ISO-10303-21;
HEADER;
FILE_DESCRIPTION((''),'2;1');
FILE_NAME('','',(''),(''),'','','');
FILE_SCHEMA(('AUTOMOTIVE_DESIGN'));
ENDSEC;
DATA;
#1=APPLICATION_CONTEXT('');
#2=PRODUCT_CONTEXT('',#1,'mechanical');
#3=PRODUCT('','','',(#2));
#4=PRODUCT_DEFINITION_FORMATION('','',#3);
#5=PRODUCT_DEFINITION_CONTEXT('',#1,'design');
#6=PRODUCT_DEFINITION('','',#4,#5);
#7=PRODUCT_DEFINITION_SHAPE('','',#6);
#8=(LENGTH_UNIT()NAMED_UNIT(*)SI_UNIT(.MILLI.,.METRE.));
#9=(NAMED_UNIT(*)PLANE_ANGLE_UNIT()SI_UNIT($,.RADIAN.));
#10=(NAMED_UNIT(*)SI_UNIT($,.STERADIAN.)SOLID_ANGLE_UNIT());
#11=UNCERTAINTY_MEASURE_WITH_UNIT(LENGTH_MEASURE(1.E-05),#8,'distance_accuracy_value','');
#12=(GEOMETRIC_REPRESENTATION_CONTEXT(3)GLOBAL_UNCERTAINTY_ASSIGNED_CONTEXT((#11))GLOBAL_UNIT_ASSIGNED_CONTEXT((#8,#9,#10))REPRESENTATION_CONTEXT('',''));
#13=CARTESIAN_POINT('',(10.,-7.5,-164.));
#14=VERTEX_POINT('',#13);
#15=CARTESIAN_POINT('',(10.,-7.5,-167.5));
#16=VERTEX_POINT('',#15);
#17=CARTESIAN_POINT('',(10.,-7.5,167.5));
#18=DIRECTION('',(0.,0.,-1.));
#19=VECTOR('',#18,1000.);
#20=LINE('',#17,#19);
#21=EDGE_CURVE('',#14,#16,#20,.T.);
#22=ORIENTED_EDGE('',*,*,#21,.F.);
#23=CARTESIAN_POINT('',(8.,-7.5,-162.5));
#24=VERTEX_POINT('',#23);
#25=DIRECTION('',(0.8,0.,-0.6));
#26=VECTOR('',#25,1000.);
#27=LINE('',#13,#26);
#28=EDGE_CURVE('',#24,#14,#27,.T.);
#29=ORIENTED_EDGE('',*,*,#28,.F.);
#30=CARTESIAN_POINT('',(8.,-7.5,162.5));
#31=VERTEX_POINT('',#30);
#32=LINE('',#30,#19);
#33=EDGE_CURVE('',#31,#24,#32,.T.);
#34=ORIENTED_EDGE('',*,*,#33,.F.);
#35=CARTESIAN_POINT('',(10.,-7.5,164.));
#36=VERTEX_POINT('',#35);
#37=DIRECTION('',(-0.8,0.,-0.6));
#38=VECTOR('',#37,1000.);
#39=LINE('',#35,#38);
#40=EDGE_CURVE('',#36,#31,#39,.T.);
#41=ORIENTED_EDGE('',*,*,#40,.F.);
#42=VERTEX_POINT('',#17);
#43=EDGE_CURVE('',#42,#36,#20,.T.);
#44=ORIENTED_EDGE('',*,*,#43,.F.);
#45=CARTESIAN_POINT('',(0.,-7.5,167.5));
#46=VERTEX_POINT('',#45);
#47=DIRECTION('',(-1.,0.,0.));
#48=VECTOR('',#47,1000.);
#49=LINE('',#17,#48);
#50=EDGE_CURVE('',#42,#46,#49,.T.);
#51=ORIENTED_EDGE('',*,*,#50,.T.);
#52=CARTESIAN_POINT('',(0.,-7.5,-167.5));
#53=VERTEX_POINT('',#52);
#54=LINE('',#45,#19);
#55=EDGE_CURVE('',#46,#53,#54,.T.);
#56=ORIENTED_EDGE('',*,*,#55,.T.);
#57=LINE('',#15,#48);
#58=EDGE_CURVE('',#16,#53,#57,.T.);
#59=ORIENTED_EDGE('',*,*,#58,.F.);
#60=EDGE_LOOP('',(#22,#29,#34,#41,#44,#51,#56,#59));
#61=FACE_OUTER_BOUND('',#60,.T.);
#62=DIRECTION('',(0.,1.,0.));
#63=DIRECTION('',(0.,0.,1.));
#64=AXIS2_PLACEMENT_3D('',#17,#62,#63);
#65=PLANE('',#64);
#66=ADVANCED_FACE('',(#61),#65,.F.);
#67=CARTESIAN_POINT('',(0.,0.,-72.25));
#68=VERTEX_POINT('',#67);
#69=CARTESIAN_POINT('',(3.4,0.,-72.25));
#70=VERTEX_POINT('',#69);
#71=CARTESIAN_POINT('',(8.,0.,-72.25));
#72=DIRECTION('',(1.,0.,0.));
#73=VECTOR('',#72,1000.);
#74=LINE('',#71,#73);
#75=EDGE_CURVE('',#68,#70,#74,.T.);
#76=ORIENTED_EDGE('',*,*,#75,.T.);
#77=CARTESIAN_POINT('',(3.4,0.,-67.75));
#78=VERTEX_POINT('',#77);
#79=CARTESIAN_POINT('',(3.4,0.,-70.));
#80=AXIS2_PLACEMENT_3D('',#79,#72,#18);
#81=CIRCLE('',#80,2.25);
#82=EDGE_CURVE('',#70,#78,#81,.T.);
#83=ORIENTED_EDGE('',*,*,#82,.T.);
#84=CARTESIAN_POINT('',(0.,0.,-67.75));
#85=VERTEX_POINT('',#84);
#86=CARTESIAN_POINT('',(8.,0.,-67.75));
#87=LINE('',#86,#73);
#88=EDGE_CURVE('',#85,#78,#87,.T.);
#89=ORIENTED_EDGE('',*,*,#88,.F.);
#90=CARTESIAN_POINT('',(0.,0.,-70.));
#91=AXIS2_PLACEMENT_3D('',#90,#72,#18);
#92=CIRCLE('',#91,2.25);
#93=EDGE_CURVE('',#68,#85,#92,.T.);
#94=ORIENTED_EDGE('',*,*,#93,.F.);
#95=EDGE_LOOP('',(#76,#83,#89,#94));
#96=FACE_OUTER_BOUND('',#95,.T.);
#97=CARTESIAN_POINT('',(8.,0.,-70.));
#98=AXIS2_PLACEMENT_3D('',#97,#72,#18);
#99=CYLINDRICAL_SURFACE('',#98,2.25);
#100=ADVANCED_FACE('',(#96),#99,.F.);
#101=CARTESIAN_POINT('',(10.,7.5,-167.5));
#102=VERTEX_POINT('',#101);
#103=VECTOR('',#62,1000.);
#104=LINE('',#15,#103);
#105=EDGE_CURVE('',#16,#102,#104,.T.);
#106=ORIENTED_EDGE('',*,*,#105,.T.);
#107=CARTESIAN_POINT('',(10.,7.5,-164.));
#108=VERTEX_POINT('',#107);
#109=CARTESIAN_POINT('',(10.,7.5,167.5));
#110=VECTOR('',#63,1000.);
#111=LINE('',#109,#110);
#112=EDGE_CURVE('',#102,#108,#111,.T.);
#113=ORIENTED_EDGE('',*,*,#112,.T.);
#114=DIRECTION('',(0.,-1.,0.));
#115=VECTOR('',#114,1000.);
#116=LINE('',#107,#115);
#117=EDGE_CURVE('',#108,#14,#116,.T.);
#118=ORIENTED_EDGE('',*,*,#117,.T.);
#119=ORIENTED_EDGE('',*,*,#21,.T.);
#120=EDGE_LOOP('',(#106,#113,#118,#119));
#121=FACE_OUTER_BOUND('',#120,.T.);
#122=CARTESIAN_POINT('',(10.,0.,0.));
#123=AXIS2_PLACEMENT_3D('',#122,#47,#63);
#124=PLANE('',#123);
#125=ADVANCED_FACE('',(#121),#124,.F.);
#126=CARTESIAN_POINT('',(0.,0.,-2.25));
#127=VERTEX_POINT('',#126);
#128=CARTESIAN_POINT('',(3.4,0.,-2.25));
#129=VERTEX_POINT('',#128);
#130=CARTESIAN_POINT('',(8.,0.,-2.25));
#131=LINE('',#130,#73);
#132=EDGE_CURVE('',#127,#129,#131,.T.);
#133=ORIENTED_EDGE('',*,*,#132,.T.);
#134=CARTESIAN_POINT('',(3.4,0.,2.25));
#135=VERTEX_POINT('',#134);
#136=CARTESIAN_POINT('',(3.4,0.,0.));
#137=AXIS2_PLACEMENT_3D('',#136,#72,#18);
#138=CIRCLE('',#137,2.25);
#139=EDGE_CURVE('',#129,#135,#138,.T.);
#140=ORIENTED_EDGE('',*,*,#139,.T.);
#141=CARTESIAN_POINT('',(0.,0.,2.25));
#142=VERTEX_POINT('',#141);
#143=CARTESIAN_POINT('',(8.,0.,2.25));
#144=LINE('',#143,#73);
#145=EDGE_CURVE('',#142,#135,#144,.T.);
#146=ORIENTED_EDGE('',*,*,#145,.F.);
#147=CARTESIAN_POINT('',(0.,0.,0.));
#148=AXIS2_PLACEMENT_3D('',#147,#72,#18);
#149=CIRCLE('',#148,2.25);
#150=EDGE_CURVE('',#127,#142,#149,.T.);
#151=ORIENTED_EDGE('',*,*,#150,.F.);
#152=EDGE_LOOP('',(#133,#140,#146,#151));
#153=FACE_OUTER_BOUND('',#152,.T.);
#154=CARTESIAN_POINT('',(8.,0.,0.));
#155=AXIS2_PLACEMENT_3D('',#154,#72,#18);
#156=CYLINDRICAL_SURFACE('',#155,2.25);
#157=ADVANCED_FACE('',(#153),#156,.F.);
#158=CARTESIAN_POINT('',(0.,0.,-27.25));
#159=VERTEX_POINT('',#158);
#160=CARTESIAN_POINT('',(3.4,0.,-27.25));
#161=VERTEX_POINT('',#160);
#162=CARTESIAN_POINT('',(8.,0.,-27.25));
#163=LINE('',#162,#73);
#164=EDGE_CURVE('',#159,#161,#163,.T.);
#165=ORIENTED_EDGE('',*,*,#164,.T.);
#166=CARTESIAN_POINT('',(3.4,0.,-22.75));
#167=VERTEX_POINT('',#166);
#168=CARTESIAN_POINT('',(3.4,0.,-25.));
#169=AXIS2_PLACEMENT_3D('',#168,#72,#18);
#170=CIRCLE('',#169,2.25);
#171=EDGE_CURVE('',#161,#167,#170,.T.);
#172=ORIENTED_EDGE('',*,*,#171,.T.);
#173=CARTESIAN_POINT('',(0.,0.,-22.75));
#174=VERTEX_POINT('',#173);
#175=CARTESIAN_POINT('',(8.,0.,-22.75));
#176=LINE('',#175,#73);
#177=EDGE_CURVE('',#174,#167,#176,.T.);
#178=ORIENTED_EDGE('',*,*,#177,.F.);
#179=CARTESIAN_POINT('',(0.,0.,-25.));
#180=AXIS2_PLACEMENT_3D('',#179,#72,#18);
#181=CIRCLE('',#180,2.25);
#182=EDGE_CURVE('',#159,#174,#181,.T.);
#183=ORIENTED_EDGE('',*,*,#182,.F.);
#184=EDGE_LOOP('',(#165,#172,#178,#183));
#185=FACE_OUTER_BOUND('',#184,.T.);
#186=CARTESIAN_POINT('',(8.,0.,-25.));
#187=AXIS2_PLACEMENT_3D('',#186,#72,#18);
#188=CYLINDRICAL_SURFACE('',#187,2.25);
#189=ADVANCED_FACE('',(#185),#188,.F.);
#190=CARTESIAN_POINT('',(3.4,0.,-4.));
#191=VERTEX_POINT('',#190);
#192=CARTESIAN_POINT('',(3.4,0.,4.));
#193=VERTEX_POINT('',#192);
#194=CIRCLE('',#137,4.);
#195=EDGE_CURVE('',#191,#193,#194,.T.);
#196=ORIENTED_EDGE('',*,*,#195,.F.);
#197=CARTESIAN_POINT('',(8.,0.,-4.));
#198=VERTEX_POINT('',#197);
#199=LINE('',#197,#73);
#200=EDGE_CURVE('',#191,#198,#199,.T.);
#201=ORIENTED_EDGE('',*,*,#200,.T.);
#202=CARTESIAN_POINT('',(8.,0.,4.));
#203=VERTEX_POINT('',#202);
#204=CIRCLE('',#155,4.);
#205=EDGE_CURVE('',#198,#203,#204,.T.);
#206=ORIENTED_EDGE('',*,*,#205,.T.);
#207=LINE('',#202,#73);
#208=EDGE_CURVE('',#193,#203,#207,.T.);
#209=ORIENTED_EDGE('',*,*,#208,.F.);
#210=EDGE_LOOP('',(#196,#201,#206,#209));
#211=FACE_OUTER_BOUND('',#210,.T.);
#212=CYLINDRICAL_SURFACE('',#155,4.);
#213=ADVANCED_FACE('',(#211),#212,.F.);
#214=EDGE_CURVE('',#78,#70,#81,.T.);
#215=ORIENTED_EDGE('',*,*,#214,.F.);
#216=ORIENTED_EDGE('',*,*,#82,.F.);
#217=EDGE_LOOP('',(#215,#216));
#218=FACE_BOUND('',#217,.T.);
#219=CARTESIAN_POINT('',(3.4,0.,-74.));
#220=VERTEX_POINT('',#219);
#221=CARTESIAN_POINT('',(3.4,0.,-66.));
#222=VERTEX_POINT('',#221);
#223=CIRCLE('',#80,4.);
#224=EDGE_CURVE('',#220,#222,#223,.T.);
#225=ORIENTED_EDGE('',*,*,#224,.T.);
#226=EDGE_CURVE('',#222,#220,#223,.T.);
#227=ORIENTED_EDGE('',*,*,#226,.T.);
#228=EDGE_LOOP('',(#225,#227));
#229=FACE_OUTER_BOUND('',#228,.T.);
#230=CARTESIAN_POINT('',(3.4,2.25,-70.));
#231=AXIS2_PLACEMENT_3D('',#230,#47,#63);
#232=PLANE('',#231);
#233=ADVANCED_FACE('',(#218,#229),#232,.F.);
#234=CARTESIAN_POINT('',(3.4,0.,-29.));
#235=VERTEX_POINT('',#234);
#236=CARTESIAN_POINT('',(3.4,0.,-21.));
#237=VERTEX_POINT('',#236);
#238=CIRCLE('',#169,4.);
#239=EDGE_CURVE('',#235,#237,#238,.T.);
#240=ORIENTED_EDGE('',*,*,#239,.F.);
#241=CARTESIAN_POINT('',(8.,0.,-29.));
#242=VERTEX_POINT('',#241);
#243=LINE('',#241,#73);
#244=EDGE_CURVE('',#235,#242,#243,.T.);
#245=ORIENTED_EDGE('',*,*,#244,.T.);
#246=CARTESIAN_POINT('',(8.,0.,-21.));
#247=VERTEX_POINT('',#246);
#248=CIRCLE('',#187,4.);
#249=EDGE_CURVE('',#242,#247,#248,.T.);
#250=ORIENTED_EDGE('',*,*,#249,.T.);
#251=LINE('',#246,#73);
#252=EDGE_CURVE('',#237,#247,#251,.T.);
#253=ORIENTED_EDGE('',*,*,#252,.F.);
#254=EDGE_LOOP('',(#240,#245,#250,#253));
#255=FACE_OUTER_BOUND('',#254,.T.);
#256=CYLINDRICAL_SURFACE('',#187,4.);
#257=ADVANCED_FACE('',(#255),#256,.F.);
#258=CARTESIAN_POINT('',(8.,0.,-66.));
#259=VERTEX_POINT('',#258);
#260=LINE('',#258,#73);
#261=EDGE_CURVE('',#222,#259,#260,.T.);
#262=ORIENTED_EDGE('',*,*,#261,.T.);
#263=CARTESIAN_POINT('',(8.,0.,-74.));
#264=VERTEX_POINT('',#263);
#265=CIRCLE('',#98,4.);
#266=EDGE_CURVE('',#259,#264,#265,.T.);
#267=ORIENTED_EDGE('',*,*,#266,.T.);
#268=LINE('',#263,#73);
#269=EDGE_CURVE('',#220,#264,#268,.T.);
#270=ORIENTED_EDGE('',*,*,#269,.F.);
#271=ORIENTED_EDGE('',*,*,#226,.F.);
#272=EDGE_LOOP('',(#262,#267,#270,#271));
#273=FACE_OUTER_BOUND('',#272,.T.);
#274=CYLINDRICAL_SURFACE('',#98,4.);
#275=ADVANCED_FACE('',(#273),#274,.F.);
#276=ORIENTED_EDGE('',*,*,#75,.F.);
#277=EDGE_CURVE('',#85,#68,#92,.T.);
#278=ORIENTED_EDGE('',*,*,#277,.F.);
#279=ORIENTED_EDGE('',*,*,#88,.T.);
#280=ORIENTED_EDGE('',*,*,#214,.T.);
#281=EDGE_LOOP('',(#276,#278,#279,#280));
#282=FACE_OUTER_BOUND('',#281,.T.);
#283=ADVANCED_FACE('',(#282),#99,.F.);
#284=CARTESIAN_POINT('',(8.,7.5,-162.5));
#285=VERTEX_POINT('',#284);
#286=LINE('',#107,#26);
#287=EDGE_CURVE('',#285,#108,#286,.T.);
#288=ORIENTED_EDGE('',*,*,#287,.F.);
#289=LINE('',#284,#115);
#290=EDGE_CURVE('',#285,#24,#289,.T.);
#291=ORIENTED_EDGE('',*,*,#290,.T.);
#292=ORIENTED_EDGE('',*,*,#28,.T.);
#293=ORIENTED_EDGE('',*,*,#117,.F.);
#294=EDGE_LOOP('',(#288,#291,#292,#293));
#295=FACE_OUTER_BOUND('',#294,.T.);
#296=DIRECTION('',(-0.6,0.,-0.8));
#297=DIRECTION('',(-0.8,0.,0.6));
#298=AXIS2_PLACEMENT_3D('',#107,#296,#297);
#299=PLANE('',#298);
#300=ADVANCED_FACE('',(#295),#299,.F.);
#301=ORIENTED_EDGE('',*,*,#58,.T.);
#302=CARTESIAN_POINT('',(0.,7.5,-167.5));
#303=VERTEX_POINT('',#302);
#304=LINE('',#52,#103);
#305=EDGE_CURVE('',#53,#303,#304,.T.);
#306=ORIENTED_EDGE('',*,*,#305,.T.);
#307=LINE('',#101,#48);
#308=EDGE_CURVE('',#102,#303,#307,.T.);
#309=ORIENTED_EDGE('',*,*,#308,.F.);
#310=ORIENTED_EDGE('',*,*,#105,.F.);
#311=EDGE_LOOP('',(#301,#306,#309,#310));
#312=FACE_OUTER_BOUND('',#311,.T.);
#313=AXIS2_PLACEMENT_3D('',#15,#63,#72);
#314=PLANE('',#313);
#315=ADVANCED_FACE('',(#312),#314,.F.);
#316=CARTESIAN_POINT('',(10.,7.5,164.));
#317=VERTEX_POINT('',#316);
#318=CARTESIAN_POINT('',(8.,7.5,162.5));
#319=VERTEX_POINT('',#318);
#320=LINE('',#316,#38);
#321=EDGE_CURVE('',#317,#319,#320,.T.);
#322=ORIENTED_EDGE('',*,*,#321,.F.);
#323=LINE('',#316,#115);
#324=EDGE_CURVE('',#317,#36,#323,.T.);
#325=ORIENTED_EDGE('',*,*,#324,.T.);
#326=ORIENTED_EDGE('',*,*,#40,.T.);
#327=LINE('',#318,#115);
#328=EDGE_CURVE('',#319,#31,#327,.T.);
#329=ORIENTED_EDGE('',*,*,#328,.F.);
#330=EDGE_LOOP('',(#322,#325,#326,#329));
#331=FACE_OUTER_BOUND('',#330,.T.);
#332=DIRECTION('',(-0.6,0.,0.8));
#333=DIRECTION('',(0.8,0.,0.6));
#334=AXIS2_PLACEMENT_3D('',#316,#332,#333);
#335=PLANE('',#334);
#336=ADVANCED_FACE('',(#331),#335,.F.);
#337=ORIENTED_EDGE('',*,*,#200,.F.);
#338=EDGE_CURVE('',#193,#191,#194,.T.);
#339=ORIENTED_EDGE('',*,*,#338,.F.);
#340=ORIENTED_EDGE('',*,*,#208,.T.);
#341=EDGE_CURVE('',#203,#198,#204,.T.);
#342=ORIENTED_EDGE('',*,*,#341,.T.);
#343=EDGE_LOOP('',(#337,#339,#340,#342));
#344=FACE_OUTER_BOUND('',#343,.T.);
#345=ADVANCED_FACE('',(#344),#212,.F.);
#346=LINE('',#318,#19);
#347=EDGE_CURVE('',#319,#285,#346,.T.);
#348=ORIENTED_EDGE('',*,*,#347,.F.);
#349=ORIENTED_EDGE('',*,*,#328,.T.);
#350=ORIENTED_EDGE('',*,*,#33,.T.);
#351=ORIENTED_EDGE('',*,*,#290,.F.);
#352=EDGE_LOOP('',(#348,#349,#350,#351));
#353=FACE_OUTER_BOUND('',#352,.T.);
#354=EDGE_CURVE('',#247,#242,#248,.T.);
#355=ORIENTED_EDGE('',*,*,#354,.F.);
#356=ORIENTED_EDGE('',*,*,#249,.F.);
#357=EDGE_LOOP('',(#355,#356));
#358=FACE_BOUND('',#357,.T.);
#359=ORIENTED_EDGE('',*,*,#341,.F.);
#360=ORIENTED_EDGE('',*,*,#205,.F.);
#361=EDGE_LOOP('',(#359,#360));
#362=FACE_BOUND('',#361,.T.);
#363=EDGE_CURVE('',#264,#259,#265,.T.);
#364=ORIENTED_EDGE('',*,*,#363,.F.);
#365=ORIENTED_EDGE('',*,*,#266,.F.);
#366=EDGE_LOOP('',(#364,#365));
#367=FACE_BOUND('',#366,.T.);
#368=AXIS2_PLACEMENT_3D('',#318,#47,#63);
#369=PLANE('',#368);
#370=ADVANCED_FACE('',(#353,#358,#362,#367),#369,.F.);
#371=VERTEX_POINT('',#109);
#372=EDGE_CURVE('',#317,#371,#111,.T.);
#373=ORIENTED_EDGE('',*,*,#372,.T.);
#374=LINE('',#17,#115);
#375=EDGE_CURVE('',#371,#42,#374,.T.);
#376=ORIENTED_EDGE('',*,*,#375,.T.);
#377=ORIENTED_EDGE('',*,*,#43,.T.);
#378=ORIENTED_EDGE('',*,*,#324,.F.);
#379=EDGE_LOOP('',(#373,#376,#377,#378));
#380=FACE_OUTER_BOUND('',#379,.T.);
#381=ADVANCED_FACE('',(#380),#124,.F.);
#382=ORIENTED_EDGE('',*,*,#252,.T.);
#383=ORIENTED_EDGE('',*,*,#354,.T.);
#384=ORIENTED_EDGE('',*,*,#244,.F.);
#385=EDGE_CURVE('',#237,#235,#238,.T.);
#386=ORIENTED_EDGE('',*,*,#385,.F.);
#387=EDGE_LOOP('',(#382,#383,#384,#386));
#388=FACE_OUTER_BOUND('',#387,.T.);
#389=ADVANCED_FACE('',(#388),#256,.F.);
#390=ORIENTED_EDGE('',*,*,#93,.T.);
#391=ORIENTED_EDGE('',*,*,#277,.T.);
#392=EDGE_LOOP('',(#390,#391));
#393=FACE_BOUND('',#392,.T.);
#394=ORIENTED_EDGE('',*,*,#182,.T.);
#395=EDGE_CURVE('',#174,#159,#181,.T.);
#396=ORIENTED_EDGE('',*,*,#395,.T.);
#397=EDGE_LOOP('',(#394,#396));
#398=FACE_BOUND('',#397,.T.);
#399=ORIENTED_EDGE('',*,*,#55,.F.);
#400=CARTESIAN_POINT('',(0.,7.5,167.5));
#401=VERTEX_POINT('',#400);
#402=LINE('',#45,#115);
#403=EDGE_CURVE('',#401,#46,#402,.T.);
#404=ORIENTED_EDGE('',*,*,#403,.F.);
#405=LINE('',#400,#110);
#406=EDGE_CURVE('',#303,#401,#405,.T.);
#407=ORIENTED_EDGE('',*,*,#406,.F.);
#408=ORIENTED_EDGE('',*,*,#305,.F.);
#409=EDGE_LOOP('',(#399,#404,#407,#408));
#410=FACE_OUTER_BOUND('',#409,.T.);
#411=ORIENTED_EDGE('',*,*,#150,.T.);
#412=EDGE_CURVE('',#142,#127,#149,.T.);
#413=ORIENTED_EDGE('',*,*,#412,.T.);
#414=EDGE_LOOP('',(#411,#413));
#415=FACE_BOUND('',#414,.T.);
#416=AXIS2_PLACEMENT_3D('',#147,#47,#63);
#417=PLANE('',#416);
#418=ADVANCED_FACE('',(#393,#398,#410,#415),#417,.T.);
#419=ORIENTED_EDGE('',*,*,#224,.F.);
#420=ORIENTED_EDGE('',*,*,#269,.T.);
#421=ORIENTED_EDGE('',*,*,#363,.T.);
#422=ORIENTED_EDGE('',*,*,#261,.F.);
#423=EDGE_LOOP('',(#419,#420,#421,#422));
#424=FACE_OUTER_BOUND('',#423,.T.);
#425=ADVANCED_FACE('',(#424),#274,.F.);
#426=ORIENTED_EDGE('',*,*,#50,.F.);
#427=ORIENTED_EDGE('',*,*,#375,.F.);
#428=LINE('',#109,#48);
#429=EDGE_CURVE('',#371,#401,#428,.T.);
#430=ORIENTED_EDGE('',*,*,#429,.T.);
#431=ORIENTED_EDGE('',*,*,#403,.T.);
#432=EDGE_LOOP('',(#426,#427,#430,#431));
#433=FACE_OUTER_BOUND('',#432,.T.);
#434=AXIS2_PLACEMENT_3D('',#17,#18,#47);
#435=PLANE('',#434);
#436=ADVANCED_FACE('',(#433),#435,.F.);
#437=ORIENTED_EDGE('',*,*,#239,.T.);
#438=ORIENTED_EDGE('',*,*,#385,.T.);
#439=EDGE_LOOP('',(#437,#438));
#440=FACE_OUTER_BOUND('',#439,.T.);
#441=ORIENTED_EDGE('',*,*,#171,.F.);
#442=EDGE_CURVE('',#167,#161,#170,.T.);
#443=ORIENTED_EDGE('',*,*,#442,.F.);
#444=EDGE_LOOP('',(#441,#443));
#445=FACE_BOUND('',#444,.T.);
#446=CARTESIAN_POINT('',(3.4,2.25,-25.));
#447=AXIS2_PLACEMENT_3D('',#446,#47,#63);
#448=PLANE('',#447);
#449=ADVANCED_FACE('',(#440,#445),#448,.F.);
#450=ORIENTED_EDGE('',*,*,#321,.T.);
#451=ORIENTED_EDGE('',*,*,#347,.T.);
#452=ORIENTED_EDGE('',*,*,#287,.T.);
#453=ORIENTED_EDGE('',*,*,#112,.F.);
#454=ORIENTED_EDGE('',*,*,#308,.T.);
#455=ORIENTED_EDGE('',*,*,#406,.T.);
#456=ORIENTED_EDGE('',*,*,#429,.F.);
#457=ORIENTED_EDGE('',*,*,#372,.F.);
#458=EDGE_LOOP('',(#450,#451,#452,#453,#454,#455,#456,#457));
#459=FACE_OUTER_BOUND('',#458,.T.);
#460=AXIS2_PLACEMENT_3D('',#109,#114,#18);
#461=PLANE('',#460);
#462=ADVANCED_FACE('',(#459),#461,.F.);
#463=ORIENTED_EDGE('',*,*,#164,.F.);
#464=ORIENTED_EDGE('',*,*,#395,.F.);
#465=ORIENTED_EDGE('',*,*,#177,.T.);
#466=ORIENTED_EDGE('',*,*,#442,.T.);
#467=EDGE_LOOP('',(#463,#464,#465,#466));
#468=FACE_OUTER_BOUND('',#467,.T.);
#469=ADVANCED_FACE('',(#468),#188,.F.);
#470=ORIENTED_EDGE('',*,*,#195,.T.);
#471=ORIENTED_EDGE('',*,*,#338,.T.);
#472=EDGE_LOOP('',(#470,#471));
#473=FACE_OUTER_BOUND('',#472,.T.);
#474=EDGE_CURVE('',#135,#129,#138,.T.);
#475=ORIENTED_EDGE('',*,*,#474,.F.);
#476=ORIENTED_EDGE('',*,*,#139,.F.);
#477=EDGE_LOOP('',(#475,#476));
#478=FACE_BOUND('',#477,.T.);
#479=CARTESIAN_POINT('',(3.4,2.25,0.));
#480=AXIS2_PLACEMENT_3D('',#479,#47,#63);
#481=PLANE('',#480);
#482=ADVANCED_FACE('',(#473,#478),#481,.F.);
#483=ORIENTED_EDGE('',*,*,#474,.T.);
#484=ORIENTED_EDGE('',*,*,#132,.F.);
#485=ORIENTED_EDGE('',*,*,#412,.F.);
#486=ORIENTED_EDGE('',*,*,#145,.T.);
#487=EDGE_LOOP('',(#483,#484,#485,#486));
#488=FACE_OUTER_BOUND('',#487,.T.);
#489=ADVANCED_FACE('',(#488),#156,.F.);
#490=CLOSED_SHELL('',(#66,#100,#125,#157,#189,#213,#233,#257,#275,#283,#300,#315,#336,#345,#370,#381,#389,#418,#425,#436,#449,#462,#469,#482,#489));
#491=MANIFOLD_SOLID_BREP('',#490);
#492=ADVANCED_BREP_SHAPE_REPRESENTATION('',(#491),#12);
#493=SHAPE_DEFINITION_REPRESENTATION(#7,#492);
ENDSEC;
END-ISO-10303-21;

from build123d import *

# Parameters (mm, degrees)
SKETCH1_W                                            = 335
SKETCH1_H                                            = 15
BOSS_EXTRUDE1_DEPTH                                  = 10
CUT_EXTRUDE2_DEPTH                                   = 169.467355888
CBORE_FOR_M4_HEXAGON_SOCKET_HEAD_CAP_SCR_D           = 4.5
CBORE_FOR_M4_HEXAGON_SOCKET_HEAD_CAP_SCR_CBORE_D     = 8
CBORE_FOR_M4_HEXAGON_SOCKET_HEAD_CAP_SCR_CBORE_DEPTH = 4.6


with BuildPart() as part:
    # Sketch1 → Boss-Extrude1 (new body)
    with BuildSketch(Plane(origin=(0, 0, 0), x_dir=(0, 0, -1), z_dir=(1, 0, 0))):
        Rectangle(SKETCH1_W, SKETCH1_H)
    extrude(amount=BOSS_EXTRUDE1_DEPTH)

    # Sketch2 → Cut-Extrude2 (cut, through all)
    with BuildSketch(Plane.XZ.offset(7.5)):
        Polygon((8, 162.5), (8, -162.5), (10, -164), (10, 0), (10, 164), align=None)
    extrude(amount=-CUT_EXTRUDE2_DEPTH, mode=Mode.SUBTRACT)

    # CBORE for M4 Hexagon socket head cap screws1 (through all)
    with Locations(Plane(origin=(8, 0, 0), x_dir=(0, 0, -1), z_dir=(1, 0, 0))):
        with Locations((0, 0), (70, 0), (25, 0)):
            CounterBoreHole(CBORE_FOR_M4_HEXAGON_SOCKET_HEAD_CAP_SCR_D / 2, CBORE_FOR_M4_HEXAGON_SOCKET_HEAD_CAP_SCR_CBORE_D / 2, CBORE_FOR_M4_HEXAGON_SOCKET_HEAD_CAP_SCR_CBORE_DEPTH)


solid = part.part
